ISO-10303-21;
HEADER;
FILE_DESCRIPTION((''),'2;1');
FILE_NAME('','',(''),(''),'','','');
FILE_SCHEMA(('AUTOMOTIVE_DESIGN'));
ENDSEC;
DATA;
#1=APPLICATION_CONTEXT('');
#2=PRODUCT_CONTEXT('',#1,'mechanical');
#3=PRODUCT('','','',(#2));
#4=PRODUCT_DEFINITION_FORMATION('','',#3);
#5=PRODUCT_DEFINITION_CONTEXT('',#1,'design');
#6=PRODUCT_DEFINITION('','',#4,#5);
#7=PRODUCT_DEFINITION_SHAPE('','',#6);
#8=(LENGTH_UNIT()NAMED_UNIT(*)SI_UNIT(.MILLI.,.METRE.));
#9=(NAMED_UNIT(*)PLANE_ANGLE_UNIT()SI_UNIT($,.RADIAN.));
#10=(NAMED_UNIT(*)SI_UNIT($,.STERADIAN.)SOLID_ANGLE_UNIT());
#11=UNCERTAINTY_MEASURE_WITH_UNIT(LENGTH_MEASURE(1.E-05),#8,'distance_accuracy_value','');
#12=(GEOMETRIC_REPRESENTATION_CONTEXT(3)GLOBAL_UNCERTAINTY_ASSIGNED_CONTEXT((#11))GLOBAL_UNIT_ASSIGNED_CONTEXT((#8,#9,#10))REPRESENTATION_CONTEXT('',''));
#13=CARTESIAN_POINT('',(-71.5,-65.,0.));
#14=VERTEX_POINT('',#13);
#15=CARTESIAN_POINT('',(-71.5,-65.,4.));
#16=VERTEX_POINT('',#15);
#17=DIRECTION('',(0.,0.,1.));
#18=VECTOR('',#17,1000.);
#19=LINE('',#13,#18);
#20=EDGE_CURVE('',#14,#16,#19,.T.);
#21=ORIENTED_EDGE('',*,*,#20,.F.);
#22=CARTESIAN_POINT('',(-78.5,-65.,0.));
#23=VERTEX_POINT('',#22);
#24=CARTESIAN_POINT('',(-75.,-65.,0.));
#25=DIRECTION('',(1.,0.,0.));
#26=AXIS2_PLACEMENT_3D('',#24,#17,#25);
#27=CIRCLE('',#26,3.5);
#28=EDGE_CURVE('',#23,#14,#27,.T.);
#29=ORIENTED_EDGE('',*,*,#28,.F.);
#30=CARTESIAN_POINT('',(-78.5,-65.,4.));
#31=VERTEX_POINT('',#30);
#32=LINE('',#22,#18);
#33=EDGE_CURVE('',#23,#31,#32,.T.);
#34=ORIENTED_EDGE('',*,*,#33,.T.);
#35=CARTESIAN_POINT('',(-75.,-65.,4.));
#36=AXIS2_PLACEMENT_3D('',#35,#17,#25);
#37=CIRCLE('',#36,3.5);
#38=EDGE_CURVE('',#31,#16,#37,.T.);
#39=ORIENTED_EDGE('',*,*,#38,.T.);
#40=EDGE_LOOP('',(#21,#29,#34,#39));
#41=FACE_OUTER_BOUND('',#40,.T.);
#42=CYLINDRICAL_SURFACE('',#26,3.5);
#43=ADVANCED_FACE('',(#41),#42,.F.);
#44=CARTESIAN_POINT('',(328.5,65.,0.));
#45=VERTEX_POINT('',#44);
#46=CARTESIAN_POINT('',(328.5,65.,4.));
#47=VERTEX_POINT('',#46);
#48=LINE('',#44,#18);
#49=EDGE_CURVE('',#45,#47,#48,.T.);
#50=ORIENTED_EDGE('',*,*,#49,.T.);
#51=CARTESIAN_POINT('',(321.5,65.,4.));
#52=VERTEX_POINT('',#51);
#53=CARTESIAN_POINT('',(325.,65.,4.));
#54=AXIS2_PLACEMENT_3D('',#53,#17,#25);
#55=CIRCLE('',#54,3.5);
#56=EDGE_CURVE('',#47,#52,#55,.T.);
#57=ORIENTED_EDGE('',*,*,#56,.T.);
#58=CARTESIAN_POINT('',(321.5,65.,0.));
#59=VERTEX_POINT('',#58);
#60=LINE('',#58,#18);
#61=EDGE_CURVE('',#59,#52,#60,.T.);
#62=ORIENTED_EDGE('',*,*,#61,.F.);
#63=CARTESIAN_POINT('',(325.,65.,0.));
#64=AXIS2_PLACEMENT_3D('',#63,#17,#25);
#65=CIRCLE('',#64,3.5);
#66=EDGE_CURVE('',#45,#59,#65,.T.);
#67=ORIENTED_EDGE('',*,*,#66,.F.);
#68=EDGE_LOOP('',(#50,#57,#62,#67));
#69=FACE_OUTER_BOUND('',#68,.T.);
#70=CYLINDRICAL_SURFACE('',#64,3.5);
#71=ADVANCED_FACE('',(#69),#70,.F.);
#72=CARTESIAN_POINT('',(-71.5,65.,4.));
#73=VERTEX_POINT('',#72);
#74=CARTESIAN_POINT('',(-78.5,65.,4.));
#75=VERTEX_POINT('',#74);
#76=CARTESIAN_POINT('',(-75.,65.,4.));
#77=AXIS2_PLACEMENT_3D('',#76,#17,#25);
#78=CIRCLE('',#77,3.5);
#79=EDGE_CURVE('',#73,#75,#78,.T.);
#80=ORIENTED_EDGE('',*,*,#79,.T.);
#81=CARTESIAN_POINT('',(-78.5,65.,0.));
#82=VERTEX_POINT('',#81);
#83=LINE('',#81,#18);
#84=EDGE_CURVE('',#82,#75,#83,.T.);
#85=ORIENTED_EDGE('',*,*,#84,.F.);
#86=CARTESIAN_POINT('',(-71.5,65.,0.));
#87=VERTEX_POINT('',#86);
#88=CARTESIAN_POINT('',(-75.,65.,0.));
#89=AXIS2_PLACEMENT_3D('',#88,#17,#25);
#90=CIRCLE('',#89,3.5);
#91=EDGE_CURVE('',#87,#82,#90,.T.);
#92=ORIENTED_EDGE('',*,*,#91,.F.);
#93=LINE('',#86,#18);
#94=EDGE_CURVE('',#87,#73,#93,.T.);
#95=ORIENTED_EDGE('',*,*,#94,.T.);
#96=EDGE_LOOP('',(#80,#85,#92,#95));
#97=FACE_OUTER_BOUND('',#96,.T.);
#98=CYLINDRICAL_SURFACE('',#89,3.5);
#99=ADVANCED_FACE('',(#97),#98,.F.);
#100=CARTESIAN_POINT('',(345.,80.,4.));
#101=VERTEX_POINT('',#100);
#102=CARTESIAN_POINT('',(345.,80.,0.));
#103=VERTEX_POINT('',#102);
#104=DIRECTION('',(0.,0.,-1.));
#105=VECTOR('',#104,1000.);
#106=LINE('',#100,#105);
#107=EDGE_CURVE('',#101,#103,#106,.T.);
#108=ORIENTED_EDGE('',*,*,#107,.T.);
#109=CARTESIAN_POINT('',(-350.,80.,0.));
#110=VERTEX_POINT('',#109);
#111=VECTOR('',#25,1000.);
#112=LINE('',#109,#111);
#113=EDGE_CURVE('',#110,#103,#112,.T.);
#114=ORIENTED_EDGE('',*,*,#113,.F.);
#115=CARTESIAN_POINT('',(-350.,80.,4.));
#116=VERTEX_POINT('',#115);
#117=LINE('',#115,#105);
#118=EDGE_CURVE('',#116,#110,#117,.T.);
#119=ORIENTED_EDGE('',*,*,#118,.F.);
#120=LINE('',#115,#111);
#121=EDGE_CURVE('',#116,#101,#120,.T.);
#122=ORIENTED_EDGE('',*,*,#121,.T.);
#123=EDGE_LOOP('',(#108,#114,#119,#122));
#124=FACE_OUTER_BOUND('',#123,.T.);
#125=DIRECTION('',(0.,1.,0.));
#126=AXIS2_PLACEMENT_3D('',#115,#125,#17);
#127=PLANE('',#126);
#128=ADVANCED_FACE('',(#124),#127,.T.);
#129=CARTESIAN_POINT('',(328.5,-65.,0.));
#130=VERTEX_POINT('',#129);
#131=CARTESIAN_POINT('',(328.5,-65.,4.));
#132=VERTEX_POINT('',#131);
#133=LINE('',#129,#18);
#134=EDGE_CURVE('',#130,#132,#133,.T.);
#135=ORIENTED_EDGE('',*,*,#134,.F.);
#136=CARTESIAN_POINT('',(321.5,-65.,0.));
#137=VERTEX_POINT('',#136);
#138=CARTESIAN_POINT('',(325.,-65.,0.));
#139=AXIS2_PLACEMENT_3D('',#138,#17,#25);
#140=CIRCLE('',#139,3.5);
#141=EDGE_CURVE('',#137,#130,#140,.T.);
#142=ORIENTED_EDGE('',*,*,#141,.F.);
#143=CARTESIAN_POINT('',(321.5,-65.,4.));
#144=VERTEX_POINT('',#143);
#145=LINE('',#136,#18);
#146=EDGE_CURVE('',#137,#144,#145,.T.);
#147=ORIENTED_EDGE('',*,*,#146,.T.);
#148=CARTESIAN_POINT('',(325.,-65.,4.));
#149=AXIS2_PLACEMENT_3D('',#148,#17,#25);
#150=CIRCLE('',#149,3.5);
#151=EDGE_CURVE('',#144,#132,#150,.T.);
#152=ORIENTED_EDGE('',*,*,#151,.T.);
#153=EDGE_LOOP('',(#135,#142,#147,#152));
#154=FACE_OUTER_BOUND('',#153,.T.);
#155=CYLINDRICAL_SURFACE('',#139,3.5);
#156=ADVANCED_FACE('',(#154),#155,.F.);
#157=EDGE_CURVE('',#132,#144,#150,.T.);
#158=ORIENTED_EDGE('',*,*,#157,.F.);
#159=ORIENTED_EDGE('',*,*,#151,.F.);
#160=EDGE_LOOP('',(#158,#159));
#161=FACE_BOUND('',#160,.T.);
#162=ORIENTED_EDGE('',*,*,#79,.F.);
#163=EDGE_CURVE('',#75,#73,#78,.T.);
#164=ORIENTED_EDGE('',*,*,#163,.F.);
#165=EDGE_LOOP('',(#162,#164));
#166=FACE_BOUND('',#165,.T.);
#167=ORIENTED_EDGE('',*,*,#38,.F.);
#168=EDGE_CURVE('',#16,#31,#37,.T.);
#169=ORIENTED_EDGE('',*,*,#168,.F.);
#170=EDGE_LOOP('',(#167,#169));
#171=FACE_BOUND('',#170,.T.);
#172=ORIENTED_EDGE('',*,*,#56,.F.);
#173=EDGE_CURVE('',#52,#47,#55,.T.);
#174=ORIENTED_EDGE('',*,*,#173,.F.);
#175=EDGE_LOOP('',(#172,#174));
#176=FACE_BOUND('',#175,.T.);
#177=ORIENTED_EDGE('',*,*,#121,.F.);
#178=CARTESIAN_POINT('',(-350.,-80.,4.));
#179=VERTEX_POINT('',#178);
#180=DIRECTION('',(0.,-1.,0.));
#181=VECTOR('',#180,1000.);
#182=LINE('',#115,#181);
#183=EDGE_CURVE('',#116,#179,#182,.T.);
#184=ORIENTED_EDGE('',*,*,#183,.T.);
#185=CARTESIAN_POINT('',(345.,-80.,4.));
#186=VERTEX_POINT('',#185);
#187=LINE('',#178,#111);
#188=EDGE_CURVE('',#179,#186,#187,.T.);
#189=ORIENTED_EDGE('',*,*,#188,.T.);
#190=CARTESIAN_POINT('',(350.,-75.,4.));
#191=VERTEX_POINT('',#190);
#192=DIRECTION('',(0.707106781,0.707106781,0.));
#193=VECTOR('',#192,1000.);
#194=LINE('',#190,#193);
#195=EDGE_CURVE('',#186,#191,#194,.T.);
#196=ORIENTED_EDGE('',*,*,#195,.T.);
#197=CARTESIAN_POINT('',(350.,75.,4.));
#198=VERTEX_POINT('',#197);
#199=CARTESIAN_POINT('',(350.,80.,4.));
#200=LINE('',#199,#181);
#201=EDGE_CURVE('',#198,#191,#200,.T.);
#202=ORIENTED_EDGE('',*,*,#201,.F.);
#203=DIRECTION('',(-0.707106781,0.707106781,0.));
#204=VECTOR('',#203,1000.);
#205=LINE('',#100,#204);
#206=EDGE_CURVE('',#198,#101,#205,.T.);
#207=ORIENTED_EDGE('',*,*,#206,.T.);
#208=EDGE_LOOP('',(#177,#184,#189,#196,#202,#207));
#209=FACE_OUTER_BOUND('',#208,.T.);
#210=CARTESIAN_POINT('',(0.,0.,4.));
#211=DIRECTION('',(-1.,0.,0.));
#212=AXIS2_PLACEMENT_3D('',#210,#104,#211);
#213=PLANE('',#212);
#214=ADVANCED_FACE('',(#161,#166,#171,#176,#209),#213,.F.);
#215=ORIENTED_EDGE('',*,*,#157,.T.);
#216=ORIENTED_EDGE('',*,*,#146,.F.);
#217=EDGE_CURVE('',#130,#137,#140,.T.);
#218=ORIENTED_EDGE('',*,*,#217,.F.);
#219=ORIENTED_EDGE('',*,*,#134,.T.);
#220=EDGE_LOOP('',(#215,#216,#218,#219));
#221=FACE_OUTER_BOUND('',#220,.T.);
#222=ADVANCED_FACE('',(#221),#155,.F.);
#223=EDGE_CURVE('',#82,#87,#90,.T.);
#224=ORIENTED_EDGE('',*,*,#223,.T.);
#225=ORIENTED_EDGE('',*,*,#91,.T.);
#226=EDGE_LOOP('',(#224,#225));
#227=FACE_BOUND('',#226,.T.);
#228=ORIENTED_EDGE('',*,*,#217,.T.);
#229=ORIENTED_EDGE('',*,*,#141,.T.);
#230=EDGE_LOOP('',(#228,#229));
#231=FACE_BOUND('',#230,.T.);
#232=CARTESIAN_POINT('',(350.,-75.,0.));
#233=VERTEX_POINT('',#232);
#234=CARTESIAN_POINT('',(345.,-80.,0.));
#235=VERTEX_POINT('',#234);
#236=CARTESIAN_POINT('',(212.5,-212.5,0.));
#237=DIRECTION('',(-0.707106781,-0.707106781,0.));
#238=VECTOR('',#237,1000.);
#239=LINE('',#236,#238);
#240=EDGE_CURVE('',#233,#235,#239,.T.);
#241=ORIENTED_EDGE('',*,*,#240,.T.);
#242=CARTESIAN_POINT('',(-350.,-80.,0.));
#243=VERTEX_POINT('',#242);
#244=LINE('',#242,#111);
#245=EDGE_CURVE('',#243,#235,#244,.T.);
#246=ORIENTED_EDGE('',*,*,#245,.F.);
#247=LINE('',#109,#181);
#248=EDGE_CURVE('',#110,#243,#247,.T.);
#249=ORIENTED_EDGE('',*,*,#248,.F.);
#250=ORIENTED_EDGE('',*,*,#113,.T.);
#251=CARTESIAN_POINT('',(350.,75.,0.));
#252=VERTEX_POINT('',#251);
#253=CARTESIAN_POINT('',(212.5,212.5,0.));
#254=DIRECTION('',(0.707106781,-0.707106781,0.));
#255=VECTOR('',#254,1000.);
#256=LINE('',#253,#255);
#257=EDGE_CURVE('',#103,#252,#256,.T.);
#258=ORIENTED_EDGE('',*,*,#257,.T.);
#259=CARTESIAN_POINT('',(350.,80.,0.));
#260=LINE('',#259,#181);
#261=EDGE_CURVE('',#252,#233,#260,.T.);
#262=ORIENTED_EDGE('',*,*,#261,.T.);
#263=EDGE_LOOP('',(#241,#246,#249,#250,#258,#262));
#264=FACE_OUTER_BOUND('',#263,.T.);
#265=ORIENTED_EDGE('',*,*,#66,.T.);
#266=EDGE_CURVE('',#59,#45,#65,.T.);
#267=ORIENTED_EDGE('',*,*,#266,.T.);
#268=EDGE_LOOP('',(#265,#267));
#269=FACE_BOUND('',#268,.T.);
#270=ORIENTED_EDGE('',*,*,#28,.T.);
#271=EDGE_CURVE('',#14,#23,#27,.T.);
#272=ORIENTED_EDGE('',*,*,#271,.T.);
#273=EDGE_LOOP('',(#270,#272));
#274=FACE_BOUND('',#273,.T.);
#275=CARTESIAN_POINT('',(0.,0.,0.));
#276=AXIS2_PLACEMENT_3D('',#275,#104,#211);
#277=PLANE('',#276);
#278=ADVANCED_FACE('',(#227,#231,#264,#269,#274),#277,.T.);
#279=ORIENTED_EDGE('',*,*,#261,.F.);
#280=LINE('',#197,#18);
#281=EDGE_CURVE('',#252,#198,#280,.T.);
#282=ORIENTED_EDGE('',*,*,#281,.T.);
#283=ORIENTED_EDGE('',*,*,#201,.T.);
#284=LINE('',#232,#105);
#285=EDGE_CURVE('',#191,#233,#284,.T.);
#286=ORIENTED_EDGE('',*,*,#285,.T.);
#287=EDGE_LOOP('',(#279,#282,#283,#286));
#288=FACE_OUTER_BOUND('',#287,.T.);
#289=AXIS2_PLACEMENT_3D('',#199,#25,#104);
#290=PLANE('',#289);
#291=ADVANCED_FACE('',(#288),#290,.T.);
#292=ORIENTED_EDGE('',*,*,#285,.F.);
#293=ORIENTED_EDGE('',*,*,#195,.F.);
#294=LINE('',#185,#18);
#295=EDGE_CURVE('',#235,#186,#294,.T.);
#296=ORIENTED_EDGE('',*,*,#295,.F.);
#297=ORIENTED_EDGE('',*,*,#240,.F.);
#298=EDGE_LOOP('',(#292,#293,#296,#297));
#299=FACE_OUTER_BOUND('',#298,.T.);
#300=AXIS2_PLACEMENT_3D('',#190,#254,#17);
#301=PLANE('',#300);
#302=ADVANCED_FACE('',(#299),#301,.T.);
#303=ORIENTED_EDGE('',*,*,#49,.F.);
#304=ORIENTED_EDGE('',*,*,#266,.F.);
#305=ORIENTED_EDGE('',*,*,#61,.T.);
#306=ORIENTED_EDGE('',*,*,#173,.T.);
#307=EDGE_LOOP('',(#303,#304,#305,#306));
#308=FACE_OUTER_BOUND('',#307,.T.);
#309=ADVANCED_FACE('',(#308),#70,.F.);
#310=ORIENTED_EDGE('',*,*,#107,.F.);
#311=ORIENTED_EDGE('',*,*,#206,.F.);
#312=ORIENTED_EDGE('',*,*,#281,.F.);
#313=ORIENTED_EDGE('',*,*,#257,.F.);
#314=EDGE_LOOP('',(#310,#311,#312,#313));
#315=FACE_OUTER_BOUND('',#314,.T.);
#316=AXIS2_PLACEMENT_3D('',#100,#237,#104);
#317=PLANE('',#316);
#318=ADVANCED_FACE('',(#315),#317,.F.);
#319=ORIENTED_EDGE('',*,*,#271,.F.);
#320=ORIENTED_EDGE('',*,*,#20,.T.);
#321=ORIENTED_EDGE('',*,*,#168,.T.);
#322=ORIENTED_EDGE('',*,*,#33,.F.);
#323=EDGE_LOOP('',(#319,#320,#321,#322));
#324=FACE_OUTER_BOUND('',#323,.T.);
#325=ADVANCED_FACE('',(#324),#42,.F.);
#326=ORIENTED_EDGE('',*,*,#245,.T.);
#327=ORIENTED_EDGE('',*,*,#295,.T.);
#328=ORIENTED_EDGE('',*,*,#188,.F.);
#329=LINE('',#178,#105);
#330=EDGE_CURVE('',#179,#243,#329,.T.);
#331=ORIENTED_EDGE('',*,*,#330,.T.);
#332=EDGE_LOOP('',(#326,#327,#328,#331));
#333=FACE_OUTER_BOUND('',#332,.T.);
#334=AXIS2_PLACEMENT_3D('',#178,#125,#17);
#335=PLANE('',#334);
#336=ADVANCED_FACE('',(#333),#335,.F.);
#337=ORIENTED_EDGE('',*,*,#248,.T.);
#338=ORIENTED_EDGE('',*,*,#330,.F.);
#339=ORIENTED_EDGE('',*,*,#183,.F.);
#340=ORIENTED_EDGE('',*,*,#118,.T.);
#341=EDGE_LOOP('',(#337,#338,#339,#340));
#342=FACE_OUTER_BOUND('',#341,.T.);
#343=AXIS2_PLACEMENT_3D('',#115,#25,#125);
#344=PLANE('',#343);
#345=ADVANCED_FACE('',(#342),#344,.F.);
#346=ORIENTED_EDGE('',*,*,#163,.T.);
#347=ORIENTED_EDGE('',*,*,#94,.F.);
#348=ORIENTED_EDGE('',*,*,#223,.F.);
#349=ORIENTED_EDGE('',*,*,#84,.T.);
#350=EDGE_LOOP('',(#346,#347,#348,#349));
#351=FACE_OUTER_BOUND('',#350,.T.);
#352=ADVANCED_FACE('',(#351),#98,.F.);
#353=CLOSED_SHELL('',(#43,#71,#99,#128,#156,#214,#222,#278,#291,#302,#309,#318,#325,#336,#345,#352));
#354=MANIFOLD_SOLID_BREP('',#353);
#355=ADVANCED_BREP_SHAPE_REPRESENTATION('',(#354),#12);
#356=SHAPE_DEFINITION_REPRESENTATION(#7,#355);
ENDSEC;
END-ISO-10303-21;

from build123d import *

# Parameters (mm, degrees)
SKETCH1_W           = 700
SKETCH1_H           = 160
BOSS_EXTRUDE1_DEPTH = 4
SKETCH2_R           = 3.5
CUT_EXTRUDE1_DEPTH  = 4
CHAMFER1_SIZE       = 5


with BuildPart() as part:
    # Sketch1 → Boss-Extrude1 (new body)
    with BuildSketch(Plane.XY):
        Rectangle(SKETCH1_W, SKETCH1_H)
    extrude(amount=BOSS_EXTRUDE1_DEPTH)

    # Sketch2 → Cut-Extrude1 (cut)
    with BuildSketch(Plane.XY.offset(4)):
        with Locations((-75, 65)):
            Circle(SKETCH2_R)
        with Locations((325, 65)):
            Circle(SKETCH2_R)
        with Locations((325, -65)):
            Circle(SKETCH2_R)
        with Locations((-75, -65)):
            Circle(SKETCH2_R)
    extrude(amount=-CUT_EXTRUDE1_DEPTH, mode=Mode.SUBTRACT)

    # Chamfer1
    chamfer1_edges = [part.edges().sort_by_distance(p)[0] for p in [
        (350, 80, 2),
        (350, -80, 2),
    ]]
    chamfer(chamfer1_edges, length=CHAMFER1_SIZE)


solid = part.part
